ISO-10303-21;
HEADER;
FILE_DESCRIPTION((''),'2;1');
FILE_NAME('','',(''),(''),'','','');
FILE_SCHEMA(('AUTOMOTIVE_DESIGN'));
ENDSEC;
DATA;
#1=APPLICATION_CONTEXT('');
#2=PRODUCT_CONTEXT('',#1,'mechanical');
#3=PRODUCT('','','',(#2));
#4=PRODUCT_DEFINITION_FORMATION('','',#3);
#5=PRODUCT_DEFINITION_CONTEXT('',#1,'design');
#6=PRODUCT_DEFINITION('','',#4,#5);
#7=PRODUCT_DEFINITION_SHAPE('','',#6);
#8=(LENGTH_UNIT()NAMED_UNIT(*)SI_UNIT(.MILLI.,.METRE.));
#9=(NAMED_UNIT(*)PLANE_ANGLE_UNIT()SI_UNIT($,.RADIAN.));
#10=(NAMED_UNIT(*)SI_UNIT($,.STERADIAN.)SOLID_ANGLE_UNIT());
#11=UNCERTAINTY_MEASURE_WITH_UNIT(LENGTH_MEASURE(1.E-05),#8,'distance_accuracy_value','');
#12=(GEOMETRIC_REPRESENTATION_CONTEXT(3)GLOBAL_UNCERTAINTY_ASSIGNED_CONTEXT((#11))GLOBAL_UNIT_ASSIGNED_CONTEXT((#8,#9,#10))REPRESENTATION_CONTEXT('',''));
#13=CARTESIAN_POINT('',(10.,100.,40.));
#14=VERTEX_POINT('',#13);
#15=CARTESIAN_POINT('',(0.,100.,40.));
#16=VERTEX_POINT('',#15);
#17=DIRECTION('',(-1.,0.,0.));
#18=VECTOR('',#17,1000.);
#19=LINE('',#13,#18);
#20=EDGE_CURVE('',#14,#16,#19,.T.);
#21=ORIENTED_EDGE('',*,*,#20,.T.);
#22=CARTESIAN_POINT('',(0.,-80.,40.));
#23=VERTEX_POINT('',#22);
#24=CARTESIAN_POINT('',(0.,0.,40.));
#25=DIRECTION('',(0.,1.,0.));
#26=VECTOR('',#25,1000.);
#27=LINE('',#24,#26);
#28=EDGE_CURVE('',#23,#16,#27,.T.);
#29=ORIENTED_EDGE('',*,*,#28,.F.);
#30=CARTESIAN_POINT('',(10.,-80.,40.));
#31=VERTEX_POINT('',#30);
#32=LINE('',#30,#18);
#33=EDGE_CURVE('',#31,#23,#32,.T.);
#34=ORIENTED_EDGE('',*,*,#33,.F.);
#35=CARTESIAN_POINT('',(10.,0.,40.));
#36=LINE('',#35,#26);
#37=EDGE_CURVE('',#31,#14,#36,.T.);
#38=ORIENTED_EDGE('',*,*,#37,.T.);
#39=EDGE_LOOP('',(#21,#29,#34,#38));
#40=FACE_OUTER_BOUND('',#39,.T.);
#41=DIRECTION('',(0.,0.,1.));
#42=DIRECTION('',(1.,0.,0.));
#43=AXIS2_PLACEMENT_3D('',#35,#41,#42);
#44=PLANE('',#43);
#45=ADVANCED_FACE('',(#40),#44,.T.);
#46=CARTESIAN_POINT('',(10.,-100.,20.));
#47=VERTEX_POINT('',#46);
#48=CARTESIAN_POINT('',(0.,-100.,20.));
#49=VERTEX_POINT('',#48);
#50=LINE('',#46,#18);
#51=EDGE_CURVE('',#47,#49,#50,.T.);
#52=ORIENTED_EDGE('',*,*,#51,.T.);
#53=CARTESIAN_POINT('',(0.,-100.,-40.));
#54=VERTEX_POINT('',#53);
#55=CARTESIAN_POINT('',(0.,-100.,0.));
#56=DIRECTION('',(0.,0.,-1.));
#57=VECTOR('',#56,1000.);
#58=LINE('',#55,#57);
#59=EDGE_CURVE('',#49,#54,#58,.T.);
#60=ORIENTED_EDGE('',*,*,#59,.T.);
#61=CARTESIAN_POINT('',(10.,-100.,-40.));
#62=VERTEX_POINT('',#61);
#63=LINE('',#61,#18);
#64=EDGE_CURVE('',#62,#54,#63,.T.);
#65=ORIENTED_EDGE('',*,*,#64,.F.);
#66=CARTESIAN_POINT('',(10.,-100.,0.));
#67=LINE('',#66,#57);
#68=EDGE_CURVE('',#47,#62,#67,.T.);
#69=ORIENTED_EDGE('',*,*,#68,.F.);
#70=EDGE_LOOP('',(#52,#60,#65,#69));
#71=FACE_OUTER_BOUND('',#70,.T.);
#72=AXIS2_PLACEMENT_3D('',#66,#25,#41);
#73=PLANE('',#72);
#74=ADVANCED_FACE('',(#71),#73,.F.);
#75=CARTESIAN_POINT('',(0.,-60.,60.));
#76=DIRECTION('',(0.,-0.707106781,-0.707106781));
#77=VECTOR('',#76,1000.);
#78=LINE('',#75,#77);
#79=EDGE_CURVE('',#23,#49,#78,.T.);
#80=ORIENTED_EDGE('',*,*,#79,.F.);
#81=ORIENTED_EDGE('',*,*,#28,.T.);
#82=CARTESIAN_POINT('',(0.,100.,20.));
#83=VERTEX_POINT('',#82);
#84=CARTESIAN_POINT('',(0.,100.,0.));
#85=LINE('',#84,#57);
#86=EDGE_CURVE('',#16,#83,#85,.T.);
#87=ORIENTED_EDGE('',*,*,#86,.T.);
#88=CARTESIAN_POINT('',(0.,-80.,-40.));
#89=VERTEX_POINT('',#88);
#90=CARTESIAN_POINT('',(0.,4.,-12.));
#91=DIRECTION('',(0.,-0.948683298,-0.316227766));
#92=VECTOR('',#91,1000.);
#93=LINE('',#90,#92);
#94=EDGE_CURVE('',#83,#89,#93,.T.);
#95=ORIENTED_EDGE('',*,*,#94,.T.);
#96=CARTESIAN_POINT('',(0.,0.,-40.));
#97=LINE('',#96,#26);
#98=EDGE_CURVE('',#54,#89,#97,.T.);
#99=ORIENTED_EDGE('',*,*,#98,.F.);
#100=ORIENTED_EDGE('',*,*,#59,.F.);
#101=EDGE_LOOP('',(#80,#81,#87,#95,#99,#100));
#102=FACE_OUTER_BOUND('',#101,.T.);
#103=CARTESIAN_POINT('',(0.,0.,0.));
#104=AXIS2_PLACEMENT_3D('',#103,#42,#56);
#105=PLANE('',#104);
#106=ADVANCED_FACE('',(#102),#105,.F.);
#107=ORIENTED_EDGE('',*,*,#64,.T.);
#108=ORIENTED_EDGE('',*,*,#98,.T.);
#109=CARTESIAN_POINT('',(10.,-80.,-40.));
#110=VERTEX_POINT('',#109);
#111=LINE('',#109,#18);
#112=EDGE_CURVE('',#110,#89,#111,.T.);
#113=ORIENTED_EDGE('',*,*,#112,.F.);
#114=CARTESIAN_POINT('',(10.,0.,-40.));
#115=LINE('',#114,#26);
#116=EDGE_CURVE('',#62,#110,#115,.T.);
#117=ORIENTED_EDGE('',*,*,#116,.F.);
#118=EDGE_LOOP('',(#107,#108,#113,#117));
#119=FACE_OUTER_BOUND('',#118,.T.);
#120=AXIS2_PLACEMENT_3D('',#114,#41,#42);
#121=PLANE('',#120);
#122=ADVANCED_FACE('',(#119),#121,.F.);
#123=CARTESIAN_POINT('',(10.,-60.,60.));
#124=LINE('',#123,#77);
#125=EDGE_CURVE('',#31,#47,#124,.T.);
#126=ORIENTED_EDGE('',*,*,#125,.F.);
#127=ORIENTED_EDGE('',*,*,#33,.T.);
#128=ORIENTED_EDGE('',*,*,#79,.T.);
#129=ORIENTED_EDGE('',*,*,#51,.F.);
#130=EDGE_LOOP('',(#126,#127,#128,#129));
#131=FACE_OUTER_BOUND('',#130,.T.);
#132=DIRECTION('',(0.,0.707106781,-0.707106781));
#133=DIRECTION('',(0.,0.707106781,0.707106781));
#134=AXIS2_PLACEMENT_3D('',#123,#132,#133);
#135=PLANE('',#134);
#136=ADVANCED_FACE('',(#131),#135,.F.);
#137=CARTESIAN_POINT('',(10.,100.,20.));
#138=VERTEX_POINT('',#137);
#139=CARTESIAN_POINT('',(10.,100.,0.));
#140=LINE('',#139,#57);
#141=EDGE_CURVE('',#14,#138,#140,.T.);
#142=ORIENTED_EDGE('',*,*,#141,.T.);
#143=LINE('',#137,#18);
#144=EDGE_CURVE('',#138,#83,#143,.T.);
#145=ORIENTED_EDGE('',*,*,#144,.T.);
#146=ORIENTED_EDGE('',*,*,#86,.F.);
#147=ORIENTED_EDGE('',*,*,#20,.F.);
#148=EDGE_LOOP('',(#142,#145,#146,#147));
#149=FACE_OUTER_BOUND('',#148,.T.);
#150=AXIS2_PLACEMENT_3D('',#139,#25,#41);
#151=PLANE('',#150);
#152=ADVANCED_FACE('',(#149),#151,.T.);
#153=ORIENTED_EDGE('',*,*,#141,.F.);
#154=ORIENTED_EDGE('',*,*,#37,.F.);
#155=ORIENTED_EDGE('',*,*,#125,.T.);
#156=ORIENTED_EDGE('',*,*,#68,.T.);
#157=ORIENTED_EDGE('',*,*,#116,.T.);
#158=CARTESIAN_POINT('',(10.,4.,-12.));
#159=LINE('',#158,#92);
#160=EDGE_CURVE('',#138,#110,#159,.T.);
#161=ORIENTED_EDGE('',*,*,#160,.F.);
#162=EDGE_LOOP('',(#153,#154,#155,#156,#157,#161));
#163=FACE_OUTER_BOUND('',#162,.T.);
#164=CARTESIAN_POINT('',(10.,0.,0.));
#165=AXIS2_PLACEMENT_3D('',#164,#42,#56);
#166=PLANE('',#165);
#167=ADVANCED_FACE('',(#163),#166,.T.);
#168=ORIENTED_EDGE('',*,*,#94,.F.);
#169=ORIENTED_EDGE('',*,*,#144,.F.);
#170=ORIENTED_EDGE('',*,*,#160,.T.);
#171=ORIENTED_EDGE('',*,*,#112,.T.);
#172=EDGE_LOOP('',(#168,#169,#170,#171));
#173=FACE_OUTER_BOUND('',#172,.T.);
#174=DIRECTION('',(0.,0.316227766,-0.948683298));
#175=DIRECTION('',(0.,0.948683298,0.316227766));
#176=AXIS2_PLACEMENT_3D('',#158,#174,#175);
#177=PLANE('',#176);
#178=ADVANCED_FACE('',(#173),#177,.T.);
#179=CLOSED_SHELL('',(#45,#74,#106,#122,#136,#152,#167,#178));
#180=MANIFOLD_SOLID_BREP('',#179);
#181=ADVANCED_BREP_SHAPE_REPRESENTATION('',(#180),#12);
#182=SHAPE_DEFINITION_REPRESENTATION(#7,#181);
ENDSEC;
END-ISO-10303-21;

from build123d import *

# Parameters (mm, degrees)
BOSS_EXTRUDE1_DEPTH = 10


with BuildPart() as part:
    # Sketch1 → Boss-Extrude1 (new body)
    with BuildSketch(Plane(origin=(0, 0, 0), x_dir=(0, 0, -1), z_dir=(1, 0, 0))):
        Polygon((40, -80), (-20, 100), (-40, 100), (-40, -80), (-20, -100), (40, -100), align=None)
    extrude(amount=BOSS_EXTRUDE1_DEPTH)


solid = part.part
